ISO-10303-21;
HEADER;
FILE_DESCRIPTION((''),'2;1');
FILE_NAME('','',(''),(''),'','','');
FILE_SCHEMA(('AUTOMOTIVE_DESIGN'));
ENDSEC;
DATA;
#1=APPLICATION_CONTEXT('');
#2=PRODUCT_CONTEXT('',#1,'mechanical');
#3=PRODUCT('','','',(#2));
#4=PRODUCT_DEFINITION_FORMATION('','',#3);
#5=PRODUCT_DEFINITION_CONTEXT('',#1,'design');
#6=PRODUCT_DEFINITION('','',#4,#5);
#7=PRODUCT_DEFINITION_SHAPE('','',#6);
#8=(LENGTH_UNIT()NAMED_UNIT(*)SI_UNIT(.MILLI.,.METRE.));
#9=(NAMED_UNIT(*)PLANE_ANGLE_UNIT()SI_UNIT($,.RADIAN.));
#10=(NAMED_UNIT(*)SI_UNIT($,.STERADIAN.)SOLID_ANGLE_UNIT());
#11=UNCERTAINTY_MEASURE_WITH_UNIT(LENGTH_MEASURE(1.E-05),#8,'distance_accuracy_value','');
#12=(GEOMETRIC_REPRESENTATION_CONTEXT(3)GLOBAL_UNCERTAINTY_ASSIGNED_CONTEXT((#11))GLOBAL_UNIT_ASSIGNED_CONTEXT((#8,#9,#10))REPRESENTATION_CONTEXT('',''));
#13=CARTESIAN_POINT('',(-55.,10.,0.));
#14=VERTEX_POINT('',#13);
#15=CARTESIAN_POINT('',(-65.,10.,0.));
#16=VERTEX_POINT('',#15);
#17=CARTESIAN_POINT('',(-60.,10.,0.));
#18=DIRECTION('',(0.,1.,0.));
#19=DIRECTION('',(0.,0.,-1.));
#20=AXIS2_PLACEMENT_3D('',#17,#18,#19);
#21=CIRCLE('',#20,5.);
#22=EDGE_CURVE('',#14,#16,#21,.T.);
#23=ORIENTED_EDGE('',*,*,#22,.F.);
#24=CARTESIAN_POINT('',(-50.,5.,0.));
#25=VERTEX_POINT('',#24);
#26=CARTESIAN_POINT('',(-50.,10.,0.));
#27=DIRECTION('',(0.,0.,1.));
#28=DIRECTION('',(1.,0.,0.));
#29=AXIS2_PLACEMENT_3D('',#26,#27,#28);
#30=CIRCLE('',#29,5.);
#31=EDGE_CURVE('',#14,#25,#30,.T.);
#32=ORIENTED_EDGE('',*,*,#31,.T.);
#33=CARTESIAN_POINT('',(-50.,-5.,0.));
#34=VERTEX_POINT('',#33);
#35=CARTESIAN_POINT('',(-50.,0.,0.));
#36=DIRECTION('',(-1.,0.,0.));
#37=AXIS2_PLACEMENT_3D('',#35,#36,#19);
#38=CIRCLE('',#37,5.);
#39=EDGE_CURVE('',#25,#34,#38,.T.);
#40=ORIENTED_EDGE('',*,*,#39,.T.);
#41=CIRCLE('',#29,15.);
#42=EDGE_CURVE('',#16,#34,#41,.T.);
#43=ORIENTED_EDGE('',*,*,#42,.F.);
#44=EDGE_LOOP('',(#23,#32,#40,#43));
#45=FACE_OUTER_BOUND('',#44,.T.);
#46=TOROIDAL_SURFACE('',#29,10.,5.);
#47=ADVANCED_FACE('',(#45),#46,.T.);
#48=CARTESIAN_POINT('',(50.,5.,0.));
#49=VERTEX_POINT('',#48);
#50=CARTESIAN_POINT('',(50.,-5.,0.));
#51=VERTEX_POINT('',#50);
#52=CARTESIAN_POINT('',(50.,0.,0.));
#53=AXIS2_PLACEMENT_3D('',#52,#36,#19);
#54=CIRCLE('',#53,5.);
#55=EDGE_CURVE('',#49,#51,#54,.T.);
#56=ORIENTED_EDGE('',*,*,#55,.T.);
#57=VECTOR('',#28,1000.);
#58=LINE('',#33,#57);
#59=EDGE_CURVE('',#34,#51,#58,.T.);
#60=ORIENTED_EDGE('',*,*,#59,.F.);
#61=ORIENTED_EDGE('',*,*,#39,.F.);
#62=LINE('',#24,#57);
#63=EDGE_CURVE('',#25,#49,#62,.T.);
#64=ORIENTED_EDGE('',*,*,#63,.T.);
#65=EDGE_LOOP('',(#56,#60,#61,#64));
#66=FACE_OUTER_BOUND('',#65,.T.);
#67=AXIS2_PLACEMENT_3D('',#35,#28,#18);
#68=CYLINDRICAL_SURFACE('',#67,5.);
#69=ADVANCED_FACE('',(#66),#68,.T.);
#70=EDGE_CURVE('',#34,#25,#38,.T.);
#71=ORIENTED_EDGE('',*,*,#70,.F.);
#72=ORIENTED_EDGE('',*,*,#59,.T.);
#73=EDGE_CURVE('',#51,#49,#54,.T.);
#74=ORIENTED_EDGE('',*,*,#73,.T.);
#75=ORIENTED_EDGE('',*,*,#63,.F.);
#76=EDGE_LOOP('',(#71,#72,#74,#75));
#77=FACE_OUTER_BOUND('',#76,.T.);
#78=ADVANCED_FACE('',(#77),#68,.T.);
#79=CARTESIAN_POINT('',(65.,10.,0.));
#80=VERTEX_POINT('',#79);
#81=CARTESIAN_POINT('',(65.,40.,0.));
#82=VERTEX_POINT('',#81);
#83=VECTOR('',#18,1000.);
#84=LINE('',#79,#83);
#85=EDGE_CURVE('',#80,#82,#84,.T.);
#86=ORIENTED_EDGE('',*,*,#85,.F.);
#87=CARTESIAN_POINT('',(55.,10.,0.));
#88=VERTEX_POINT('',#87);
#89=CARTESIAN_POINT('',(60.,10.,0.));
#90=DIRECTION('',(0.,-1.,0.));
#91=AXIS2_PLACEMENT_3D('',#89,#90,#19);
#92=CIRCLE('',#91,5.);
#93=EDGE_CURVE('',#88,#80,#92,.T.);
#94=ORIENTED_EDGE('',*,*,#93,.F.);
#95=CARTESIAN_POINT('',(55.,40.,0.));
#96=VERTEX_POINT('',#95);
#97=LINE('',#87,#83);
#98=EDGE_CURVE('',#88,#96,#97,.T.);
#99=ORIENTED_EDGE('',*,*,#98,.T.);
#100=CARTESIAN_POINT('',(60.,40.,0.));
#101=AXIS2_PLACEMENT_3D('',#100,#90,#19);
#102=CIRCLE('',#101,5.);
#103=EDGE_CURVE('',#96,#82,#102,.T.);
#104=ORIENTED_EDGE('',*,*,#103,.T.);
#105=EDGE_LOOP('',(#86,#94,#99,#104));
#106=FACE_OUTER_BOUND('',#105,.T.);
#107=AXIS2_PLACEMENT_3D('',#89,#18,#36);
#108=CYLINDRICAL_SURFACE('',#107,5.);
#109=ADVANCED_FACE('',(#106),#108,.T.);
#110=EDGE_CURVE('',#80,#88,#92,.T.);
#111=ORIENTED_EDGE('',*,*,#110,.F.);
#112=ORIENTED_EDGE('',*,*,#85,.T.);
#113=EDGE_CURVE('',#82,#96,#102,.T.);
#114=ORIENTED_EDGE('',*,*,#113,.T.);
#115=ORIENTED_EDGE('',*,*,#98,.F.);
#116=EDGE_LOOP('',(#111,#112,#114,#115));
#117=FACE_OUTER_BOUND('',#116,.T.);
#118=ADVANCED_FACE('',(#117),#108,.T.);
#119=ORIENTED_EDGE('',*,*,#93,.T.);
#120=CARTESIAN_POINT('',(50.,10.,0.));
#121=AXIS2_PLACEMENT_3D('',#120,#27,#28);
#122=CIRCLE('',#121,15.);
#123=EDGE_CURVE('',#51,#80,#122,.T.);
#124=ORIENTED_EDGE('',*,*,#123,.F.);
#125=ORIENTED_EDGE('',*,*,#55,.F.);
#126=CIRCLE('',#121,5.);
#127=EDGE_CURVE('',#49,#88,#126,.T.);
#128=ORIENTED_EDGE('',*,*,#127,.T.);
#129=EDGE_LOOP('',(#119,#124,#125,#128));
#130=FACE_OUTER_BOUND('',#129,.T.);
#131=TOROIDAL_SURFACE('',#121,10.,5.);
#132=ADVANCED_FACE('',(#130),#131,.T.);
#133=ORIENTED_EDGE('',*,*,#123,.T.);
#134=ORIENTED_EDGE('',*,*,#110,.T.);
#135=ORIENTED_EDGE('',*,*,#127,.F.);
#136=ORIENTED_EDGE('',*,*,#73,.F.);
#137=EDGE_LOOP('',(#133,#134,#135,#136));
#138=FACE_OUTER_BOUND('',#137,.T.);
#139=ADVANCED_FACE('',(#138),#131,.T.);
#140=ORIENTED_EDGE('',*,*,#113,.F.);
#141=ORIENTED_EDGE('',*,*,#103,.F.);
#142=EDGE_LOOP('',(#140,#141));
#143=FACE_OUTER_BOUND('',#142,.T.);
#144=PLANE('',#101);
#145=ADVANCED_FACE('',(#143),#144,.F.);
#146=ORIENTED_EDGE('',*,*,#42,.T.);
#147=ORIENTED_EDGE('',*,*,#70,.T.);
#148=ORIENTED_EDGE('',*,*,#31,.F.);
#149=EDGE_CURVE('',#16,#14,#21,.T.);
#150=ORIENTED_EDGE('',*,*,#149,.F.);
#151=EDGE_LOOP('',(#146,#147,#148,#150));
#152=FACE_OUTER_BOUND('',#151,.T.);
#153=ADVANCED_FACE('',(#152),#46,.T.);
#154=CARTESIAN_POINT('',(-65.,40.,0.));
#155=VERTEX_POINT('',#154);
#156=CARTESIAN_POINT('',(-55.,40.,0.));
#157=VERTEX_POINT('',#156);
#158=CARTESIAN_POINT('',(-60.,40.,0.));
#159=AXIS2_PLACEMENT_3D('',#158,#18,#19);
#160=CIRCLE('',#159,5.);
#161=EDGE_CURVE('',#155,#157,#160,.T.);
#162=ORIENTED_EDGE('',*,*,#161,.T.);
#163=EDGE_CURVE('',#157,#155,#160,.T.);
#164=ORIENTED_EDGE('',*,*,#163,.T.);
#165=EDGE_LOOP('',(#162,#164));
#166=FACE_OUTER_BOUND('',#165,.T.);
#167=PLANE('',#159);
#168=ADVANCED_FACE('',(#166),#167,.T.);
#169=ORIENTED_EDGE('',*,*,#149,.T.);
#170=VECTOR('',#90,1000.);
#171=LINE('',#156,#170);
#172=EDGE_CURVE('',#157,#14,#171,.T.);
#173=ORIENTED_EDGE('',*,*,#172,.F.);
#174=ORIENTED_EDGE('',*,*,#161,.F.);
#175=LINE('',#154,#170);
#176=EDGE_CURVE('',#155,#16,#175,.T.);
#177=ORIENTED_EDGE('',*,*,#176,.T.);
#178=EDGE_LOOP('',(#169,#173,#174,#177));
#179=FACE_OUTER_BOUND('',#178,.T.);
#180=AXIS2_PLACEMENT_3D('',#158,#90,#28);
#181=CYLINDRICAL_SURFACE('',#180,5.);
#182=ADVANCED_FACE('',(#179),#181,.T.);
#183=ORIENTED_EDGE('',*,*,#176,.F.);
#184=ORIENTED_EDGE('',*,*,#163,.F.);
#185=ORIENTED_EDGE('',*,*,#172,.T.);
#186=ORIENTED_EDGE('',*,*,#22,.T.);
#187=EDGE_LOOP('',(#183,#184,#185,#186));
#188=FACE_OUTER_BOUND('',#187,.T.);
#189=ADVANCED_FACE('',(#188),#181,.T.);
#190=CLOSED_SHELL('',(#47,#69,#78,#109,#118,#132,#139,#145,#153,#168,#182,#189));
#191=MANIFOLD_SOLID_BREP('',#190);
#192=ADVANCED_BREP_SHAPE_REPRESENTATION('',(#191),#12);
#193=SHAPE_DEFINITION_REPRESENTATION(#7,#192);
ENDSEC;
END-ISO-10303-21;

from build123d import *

# Parameters (mm, degrees)
SWEEP1_PROFILE_R = 5


with BuildPart() as part:
    # Sweep1: sweep along a path in Sketch1
    with BuildLine(Plane.XY) as sweep1_path:
        Line((-60, 40), (-60, 10))
        ThreePointArc((-60, 10), (-57.071067812, 2.928932188), (-50, 0))
        Line((-50, 0), (50, 0))
        ThreePointArc((50, 0), (57.071067812, 2.928932188), (60, 10))
        Line((60, 10), (60, 40))
    # Sweep1 profile (on start of the path) → Sweep1 (sweep)
    with BuildSketch(Plane(origin=(-60, 40, 0), x_dir=(-1, 0, 0), z_dir=(0, -1, 0))):
        Circle(SWEEP1_PROFILE_R)
    sweep(path=sweep1_path.line)


solid = part.part
